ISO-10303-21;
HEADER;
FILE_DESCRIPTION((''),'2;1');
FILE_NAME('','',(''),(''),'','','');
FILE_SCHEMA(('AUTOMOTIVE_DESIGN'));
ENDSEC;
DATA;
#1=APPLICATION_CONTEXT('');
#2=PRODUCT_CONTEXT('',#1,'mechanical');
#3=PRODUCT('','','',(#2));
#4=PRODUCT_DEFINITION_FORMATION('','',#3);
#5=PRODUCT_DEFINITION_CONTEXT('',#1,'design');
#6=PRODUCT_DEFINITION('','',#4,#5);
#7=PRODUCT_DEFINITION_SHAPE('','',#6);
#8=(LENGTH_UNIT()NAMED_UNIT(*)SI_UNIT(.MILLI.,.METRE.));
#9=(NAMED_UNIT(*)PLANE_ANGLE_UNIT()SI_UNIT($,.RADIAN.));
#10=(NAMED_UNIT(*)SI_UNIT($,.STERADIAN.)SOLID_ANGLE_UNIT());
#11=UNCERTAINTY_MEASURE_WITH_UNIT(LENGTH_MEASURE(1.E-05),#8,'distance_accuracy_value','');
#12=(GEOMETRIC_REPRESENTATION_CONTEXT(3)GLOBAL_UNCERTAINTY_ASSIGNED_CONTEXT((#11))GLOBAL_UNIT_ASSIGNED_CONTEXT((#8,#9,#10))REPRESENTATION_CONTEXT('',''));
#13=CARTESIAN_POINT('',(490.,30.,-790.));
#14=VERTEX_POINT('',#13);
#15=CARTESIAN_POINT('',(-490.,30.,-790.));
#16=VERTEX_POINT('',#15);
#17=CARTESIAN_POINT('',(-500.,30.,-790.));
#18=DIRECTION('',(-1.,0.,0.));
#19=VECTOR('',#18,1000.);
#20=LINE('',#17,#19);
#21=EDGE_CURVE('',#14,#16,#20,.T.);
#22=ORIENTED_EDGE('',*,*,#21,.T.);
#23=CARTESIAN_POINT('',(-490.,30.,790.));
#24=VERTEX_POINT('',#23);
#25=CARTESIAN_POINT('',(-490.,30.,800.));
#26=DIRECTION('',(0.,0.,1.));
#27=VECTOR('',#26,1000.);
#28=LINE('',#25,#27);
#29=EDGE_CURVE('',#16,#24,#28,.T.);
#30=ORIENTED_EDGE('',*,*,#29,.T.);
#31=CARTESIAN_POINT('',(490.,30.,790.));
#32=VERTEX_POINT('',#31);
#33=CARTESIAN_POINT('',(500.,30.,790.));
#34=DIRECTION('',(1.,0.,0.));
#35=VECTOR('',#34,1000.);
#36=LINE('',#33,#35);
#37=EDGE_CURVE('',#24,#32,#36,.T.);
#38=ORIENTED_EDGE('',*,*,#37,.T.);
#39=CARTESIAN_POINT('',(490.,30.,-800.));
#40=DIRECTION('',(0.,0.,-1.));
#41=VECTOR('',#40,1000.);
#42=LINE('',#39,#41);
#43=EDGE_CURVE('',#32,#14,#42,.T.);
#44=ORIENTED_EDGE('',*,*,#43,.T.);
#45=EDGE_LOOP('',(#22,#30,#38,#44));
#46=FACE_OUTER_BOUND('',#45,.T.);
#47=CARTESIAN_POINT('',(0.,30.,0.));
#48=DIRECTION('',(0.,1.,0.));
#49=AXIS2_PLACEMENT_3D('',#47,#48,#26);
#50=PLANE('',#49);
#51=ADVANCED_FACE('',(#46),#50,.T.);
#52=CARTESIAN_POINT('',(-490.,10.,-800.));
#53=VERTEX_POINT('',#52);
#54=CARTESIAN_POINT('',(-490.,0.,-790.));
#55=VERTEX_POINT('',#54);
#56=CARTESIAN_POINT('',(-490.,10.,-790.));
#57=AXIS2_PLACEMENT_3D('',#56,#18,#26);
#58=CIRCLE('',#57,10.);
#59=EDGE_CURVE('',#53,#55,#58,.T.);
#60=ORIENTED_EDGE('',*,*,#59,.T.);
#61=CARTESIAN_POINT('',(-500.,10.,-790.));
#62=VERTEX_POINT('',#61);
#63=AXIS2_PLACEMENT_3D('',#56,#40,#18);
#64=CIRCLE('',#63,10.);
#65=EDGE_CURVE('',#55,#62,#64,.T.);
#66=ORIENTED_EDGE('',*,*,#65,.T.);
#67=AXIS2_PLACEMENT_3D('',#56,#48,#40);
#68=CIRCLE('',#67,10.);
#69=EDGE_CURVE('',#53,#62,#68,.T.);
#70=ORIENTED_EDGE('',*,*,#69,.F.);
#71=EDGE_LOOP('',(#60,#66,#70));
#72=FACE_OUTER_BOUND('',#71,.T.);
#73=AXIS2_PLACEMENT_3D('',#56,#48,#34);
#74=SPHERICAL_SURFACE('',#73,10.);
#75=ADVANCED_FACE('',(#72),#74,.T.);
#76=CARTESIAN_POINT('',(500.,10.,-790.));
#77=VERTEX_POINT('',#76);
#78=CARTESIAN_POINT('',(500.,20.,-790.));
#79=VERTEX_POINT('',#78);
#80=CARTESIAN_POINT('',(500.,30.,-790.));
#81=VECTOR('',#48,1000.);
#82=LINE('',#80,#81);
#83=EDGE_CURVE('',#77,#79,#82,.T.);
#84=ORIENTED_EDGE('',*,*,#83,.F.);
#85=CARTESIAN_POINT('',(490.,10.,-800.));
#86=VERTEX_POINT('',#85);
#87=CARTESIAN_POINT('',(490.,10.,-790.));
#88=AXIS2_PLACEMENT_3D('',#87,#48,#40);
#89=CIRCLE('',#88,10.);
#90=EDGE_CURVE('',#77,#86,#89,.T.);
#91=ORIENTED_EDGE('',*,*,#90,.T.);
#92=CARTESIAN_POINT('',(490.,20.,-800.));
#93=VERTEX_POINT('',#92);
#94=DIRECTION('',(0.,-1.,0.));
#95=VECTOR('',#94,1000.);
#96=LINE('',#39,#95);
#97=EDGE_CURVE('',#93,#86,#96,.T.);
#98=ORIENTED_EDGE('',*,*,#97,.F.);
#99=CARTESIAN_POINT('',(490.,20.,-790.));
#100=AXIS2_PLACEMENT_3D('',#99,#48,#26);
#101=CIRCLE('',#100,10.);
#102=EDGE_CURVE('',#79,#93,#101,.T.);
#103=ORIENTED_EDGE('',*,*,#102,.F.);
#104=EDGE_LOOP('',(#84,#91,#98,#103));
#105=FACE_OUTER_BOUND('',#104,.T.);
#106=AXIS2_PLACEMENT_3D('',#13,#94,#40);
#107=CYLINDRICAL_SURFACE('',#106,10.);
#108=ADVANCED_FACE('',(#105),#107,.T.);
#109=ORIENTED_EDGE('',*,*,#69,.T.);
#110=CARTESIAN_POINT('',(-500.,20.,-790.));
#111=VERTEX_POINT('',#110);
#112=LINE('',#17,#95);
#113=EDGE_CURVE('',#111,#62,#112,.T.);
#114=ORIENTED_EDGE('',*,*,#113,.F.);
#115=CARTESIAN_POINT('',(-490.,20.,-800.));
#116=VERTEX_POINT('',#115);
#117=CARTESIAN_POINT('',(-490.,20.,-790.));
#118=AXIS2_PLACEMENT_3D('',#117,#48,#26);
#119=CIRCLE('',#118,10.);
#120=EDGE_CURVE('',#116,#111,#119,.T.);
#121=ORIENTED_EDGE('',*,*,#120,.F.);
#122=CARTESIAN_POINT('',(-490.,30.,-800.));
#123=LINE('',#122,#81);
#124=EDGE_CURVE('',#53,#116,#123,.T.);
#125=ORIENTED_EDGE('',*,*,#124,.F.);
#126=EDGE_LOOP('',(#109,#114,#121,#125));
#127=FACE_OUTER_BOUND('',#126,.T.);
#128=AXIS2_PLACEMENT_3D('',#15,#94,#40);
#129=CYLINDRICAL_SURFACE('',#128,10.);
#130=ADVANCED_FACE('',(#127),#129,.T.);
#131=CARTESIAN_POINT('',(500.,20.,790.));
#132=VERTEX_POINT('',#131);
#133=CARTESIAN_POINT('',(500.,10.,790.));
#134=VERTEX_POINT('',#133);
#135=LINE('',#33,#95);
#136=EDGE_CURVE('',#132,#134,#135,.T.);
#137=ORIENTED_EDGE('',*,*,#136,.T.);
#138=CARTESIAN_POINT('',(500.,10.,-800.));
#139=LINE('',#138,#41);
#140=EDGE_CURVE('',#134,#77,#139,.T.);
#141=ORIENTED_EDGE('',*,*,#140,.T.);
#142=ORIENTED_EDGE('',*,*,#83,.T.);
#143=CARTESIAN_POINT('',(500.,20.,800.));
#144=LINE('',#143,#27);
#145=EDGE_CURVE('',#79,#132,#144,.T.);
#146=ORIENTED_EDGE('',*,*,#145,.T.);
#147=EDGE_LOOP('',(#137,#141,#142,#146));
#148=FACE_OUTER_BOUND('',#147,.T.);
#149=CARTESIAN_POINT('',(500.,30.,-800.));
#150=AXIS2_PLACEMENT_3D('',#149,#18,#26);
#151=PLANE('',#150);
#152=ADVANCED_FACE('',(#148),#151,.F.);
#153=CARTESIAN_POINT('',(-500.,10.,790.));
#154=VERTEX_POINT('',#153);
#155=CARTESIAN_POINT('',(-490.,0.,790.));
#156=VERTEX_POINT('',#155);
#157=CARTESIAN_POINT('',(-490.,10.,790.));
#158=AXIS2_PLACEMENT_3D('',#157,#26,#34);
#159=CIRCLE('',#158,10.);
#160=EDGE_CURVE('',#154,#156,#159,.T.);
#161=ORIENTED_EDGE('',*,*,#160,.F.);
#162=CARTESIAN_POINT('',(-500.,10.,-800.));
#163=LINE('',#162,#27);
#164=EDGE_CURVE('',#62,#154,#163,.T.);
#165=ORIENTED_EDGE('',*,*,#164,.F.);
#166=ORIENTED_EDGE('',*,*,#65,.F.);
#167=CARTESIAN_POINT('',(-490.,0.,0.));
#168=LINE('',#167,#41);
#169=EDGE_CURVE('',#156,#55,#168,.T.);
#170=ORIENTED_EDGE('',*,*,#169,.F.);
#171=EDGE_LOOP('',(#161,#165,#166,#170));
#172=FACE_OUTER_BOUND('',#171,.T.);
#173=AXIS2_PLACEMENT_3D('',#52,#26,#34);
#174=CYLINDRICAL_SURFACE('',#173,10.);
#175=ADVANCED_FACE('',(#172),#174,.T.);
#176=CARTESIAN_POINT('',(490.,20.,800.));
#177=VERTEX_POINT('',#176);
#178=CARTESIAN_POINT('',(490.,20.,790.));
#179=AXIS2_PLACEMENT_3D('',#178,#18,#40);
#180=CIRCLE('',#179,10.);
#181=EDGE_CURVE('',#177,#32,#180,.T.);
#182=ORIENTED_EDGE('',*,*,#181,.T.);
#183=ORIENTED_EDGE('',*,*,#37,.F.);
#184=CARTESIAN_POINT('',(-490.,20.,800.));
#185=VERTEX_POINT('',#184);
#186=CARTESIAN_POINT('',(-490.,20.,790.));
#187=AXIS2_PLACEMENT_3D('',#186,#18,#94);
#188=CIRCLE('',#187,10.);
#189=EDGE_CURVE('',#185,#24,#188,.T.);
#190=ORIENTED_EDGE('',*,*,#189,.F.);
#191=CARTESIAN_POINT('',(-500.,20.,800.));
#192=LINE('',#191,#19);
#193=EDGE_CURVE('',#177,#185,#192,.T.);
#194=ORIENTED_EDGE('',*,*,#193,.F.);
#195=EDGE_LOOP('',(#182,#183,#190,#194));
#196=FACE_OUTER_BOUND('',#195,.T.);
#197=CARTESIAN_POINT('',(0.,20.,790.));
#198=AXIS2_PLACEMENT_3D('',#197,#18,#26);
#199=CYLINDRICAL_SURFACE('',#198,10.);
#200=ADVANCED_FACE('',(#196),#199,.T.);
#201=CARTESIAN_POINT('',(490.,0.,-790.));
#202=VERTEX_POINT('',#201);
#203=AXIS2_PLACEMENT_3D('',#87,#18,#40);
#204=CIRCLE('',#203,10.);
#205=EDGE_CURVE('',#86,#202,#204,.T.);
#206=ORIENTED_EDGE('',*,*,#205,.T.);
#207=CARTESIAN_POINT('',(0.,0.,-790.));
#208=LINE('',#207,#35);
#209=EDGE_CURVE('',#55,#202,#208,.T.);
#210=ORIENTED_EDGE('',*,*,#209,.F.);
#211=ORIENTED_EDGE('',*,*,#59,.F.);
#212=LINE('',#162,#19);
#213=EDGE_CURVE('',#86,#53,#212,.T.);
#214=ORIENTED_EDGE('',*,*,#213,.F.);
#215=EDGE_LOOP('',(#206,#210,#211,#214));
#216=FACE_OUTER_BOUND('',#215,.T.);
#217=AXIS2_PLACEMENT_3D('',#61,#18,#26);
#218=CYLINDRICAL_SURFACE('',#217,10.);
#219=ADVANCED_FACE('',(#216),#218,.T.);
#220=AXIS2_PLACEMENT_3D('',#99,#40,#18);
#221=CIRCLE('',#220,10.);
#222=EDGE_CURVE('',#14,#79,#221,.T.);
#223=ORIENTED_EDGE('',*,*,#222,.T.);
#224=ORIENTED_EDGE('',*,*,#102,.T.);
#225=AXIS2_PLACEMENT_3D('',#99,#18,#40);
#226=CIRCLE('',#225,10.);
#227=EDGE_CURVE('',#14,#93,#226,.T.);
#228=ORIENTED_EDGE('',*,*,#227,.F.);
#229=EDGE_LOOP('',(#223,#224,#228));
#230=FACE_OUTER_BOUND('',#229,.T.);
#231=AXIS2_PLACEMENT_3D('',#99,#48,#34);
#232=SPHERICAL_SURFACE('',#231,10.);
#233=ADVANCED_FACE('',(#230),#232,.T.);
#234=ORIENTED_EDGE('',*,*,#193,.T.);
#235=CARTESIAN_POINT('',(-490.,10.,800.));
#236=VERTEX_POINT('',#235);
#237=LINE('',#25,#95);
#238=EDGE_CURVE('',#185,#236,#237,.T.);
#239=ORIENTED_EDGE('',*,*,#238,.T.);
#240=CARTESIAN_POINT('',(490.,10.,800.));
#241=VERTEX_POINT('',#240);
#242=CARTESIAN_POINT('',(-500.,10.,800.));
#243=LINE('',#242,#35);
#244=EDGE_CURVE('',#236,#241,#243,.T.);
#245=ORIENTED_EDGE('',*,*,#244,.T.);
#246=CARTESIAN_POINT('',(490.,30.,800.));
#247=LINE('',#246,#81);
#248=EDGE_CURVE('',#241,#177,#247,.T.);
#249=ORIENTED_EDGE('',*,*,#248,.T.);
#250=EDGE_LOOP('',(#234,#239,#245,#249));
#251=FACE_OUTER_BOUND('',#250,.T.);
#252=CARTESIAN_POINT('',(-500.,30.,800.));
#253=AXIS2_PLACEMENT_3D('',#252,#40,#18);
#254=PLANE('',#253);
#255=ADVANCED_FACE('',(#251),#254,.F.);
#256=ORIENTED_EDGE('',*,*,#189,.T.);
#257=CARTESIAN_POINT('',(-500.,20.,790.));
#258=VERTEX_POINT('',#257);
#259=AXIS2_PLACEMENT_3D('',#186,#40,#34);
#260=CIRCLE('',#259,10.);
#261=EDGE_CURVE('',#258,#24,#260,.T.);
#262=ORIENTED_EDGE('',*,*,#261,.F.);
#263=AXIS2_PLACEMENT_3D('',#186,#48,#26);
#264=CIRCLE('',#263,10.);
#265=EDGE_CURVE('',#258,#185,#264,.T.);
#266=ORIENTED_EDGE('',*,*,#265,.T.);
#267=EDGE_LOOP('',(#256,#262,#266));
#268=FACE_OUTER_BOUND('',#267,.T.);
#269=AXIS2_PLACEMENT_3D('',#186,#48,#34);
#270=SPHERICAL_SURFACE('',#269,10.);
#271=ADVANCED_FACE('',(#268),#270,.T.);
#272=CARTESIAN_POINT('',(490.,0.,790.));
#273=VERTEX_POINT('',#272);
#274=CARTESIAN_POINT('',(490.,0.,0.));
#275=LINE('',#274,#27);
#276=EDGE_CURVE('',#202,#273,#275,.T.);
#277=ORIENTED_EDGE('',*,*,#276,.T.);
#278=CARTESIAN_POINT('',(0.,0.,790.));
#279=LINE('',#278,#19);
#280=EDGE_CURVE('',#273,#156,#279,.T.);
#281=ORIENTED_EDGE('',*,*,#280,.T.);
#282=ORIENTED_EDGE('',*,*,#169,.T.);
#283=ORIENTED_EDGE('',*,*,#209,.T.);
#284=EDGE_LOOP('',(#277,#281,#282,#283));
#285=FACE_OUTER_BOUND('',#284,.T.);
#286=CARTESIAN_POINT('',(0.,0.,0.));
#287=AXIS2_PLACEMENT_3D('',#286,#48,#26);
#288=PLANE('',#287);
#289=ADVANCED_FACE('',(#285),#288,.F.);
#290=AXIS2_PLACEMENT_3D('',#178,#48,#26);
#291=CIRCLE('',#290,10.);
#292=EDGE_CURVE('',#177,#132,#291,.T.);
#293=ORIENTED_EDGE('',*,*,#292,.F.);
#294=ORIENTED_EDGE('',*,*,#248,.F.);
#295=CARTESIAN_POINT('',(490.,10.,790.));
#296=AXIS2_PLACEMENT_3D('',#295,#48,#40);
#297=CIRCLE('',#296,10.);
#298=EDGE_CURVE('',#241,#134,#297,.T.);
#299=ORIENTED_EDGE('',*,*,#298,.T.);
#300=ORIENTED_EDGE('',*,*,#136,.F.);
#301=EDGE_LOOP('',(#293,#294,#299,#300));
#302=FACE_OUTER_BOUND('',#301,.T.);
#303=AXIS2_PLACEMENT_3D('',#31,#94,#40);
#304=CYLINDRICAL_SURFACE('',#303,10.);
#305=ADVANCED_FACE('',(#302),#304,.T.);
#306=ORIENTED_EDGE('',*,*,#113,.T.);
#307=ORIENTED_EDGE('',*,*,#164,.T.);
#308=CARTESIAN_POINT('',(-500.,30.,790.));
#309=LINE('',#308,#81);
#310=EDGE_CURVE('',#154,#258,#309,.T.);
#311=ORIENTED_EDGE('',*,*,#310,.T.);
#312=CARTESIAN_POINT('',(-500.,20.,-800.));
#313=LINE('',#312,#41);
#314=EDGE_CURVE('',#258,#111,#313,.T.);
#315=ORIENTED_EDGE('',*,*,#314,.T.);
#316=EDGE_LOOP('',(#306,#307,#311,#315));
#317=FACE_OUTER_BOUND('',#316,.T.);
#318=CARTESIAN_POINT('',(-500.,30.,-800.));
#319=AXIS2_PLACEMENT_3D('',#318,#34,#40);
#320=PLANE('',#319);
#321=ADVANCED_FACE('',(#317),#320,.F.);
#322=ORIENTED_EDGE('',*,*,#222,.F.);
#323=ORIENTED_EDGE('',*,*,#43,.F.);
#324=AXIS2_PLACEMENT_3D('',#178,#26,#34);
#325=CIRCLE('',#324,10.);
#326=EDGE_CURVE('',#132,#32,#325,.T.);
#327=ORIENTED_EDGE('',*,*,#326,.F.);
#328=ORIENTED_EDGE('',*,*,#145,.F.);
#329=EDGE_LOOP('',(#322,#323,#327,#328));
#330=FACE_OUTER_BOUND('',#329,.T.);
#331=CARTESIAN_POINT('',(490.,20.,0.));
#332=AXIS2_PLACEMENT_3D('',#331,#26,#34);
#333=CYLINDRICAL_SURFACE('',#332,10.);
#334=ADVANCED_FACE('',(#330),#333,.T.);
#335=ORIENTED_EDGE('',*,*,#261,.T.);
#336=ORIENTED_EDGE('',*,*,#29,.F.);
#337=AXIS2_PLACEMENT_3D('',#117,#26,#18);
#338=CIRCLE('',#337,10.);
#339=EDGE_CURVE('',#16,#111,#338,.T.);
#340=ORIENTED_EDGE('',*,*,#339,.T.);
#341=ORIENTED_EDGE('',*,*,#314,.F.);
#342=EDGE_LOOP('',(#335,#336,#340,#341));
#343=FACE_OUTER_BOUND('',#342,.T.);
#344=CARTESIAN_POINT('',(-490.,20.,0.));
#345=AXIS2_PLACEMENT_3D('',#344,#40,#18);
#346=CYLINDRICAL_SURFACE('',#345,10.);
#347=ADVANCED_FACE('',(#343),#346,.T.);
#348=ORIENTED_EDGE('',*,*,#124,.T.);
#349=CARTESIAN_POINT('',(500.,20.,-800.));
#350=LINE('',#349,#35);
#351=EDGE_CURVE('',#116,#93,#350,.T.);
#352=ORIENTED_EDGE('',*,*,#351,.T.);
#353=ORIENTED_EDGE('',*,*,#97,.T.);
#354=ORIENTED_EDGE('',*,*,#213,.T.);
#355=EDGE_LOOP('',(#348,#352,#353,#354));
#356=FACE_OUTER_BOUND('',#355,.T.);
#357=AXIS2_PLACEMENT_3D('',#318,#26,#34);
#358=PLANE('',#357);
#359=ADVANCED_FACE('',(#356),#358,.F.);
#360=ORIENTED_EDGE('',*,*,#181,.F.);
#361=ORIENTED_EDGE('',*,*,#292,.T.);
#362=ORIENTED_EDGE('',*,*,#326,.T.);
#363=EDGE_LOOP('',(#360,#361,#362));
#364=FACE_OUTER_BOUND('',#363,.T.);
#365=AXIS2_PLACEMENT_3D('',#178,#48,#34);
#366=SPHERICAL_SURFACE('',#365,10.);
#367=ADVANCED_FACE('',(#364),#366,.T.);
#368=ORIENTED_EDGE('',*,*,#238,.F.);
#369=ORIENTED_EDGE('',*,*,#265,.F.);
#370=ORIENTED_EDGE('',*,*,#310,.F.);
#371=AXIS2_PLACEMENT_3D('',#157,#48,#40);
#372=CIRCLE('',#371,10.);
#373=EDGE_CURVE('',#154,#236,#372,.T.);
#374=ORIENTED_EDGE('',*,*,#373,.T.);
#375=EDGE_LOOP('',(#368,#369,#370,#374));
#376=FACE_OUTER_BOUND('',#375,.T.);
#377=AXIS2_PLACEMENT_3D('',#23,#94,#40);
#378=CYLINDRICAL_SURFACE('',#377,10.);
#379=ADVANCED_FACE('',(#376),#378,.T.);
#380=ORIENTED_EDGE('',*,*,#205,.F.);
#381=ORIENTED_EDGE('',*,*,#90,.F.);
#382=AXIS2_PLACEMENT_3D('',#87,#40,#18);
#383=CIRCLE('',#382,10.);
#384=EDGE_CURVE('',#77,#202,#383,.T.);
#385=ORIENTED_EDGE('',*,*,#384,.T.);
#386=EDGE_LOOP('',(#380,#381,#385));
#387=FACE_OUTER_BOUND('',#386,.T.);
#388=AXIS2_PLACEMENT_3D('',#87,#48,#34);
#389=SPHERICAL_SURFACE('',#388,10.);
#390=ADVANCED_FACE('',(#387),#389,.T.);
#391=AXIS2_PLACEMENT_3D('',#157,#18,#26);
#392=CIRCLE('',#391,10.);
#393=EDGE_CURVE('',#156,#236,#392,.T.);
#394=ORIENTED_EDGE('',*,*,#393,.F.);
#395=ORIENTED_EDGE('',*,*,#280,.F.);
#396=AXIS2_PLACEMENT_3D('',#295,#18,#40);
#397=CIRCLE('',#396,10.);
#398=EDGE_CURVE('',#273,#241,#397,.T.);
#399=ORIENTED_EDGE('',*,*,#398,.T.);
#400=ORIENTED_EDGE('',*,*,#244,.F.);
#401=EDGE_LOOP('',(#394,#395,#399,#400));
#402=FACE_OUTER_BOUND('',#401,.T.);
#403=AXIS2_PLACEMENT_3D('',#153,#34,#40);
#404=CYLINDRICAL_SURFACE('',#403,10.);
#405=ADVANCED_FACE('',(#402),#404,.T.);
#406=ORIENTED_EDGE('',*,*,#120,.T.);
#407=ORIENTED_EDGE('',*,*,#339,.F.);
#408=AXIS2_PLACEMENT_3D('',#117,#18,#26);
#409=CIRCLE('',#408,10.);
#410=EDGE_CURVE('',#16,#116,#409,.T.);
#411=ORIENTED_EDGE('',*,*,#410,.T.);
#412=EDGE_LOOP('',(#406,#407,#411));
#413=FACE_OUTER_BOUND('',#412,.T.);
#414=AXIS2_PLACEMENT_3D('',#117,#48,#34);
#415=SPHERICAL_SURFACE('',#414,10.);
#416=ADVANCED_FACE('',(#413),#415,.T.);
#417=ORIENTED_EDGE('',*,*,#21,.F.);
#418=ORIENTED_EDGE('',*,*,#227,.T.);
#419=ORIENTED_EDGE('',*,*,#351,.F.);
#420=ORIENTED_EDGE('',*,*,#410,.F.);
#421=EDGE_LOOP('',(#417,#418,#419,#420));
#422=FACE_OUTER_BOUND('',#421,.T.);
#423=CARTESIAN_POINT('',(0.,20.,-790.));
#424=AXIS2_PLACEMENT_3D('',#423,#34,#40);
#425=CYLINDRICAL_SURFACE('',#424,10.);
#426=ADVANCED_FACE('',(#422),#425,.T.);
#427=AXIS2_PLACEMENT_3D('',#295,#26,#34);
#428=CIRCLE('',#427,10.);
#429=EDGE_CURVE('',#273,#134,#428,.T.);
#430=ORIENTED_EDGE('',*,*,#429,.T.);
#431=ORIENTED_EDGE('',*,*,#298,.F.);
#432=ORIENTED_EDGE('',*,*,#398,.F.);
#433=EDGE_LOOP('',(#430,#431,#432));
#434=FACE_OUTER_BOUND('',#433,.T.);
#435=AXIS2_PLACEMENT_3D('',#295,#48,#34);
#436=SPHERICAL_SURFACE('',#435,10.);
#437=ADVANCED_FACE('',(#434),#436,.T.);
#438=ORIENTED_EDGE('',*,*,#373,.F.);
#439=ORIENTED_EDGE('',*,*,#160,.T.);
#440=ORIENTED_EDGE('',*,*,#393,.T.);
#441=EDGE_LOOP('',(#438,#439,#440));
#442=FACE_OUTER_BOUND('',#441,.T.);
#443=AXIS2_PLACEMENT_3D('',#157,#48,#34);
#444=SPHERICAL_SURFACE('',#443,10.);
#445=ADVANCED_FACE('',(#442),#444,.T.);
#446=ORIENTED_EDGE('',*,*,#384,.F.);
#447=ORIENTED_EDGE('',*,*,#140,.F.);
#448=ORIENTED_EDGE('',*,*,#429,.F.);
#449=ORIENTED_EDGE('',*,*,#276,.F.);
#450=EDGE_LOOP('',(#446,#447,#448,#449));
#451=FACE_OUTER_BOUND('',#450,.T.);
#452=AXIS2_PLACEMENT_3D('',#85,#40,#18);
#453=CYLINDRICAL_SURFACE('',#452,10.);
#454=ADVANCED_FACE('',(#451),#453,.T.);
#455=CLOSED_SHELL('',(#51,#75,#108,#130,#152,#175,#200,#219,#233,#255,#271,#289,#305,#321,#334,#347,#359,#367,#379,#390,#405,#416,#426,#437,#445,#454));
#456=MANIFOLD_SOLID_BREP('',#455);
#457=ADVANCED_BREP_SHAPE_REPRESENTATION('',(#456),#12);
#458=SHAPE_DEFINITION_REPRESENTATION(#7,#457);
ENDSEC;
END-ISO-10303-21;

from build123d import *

# Parameters (mm, degrees)
SKETCH1_W           = 1000
SKETCH1_H           = 1600
BOSS_EXTRUDE1_DEPTH = 30
FILLET3_R           = 10


with BuildPart() as part:
    # Sketch1 → Boss-Extrude1 (new body)
    with BuildSketch(Plane(origin=(0, 0, 0), x_dir=(1, 0, 0), z_dir=(0, 1, 0))):
        Rectangle(SKETCH1_W, SKETCH1_H)
    extrude(amount=BOSS_EXTRUDE1_DEPTH)

    # Fillet3
    fillet3_edges = [part.edges().sort_by_distance(p)[0] for p in [
        (-500, 30, 0),
        (0, 30, 800),
        (500, 30, 0),
        (0, 0, 800),
        (-500, 0, 0),
        (0, 0, -800),
        (500, 0, 0),
        (0, 30, -800),
        (500, 15, 800),
        (-500, 15, 800),
        (-500, 15, -800),
        (500, 15, -800),
    ]]
    fillet(fillet3_edges, radius=FILLET3_R)


solid = part.part
